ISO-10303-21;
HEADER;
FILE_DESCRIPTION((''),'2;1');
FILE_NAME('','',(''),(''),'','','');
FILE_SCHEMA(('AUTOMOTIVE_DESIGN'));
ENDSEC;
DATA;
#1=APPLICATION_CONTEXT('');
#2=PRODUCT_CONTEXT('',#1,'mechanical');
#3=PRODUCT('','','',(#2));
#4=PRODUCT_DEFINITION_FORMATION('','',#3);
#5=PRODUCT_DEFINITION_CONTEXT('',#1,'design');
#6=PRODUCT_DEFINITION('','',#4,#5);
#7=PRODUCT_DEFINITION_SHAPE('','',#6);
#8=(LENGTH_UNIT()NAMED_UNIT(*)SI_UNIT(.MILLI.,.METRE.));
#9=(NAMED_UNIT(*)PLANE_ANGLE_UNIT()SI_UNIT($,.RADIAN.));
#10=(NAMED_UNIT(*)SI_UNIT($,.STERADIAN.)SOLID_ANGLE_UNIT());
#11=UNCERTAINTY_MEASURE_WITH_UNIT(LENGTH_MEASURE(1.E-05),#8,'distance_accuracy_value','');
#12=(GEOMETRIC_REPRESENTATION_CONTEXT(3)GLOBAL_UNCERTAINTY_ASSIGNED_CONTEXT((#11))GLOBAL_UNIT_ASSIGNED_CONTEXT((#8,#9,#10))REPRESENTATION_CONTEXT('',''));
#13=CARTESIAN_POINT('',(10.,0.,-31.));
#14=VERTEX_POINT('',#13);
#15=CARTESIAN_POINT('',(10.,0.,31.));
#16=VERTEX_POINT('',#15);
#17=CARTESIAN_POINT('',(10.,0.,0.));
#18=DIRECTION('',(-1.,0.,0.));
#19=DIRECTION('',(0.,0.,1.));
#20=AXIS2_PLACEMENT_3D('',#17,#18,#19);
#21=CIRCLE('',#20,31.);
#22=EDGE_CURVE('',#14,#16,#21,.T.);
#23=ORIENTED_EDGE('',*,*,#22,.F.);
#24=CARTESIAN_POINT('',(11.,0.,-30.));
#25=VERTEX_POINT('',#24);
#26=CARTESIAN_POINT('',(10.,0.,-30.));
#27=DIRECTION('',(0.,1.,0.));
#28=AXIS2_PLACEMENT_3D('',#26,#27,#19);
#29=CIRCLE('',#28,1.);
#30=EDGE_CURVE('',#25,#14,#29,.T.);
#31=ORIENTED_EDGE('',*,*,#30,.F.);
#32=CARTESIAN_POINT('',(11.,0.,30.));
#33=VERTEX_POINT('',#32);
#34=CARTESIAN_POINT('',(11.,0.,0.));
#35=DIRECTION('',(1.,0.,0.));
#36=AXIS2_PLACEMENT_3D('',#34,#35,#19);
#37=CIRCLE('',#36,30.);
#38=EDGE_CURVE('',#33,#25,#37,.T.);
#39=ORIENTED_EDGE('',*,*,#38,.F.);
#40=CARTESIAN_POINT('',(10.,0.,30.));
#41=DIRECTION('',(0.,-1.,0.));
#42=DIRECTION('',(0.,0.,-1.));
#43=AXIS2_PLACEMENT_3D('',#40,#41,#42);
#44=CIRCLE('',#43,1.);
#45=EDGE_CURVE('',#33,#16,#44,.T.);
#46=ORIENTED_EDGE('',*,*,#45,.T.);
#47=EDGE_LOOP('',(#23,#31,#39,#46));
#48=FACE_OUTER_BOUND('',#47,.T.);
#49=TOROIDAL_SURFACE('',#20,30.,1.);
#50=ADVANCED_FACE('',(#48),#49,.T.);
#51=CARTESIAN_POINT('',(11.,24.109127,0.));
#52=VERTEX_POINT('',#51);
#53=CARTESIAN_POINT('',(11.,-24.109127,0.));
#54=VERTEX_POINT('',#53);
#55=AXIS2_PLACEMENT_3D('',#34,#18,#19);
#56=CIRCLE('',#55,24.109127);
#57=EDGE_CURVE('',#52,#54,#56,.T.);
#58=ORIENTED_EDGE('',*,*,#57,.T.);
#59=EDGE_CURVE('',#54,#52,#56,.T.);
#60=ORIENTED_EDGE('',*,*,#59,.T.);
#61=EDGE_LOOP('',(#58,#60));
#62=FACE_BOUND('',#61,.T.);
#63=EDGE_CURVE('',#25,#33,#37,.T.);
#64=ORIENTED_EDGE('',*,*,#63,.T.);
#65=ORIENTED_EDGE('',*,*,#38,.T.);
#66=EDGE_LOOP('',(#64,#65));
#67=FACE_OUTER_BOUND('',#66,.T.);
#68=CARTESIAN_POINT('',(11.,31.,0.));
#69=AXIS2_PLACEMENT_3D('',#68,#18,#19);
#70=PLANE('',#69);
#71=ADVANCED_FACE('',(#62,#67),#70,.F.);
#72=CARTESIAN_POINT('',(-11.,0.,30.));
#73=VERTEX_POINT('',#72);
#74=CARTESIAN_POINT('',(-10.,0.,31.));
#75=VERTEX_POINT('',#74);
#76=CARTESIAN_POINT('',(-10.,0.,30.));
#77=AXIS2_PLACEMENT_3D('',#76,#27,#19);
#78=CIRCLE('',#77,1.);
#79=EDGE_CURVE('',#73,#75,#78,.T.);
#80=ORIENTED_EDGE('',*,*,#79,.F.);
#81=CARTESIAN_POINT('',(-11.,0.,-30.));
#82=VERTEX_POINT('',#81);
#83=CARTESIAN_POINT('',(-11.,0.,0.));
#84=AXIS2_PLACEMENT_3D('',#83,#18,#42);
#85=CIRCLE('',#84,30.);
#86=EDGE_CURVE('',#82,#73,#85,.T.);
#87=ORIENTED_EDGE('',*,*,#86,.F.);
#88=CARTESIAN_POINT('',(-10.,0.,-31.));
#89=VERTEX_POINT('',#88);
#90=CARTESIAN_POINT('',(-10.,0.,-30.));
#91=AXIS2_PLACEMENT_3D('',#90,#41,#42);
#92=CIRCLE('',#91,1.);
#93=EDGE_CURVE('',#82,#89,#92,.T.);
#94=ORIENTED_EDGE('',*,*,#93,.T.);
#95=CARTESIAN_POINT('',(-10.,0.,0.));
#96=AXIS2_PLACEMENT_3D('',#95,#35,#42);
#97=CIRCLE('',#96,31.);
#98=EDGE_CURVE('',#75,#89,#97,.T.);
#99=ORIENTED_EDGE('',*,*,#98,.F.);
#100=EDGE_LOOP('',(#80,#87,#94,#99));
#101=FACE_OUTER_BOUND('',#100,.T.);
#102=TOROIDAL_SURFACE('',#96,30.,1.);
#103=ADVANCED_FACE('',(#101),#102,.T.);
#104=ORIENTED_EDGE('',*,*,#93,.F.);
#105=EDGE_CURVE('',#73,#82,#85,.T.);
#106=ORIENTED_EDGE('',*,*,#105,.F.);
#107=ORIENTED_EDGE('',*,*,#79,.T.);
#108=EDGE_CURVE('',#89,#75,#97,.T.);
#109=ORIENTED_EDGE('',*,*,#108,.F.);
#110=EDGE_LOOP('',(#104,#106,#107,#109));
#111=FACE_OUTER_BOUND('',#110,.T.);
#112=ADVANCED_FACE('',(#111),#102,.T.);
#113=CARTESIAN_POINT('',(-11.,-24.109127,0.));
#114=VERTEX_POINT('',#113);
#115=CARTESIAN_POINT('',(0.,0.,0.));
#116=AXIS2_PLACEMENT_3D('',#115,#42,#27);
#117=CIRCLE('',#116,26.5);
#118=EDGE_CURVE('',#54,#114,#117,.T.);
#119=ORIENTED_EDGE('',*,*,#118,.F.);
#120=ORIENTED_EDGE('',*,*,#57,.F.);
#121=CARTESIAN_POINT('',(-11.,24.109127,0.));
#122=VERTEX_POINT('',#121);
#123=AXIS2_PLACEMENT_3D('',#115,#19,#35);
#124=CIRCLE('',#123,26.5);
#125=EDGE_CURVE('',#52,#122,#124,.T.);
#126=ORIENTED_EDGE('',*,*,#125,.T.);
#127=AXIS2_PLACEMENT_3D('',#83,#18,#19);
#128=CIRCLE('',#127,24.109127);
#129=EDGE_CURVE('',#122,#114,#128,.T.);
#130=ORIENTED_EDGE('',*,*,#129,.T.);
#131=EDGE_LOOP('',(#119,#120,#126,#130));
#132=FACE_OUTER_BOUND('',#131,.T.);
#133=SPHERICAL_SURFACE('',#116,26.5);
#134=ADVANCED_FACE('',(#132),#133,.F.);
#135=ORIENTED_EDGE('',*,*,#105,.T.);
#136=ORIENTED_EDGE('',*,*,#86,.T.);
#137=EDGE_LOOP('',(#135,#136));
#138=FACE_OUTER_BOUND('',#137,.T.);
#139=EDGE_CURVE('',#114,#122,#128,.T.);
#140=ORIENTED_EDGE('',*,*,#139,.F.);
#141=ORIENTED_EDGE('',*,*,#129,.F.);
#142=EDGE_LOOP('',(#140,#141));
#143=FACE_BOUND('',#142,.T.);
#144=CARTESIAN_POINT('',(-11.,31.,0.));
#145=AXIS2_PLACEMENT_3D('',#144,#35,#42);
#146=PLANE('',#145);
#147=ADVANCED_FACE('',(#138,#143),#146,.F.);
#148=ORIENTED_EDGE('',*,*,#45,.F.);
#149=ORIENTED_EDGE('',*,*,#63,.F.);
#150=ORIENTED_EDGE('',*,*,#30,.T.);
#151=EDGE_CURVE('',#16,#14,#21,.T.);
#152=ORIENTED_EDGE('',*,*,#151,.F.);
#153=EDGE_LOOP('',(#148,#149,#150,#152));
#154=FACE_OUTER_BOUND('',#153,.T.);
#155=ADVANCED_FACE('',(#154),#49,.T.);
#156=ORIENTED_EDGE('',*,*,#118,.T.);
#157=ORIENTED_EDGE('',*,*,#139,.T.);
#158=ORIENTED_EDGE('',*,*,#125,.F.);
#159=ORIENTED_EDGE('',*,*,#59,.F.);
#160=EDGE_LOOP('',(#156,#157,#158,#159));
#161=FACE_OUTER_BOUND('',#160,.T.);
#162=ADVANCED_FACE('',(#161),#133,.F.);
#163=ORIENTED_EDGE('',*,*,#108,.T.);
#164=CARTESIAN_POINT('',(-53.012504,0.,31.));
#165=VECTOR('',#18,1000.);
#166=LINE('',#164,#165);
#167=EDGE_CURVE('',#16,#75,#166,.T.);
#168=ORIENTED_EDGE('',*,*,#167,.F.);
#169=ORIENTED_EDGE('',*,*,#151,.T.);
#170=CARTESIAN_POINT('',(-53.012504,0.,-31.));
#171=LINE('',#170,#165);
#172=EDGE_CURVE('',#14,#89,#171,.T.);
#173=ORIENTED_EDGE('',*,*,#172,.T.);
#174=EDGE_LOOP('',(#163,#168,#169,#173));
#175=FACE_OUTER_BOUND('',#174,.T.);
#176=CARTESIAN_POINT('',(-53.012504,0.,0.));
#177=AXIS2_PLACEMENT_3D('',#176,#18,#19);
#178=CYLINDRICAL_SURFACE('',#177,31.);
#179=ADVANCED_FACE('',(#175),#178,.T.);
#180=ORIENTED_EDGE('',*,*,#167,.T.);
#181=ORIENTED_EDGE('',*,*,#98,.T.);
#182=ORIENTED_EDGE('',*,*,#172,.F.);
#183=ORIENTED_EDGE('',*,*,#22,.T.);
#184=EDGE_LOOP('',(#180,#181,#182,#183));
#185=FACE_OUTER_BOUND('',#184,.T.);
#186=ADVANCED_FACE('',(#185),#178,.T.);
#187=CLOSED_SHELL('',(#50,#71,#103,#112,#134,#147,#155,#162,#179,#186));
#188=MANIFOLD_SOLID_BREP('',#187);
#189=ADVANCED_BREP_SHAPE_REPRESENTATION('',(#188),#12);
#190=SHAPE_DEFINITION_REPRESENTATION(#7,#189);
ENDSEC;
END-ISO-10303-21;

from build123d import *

# Parameters (mm, degrees)
FILLET_1_R = 1


with BuildPart() as part:
    # 草图2 → 旋转1 (revolve)
    with BuildSketch(Plane.XY, mode=Mode.PRIVATE) as revolve_1_sk:
        with BuildLine():
            Line((-11, 31), (-11, 24.109126902))
            ThreePointArc((-11, 24.109126902), (0, 26.5), (11, 24.109126902))
            Line((11, 24.109126902), (11, 31))
            Line((11, 31), (-11, 31))
        make_face()
    revolve(revolve_1_sk.sketch.rotate(Axis((-53.012504143, 0, 0), (1, 0, 0)), 90), axis=Axis((-53.012504143, 0, 0), (1, 0, 0)))

    # 圆角1
    fillet_1_edges = [part.edges().sort_by_distance(p)[0] for p in [
        (11, 0, -31),
        (-11, 0, -31),
    ]]
    fillet(fillet_1_edges, radius=FILLET_1_R)


solid = part.part
